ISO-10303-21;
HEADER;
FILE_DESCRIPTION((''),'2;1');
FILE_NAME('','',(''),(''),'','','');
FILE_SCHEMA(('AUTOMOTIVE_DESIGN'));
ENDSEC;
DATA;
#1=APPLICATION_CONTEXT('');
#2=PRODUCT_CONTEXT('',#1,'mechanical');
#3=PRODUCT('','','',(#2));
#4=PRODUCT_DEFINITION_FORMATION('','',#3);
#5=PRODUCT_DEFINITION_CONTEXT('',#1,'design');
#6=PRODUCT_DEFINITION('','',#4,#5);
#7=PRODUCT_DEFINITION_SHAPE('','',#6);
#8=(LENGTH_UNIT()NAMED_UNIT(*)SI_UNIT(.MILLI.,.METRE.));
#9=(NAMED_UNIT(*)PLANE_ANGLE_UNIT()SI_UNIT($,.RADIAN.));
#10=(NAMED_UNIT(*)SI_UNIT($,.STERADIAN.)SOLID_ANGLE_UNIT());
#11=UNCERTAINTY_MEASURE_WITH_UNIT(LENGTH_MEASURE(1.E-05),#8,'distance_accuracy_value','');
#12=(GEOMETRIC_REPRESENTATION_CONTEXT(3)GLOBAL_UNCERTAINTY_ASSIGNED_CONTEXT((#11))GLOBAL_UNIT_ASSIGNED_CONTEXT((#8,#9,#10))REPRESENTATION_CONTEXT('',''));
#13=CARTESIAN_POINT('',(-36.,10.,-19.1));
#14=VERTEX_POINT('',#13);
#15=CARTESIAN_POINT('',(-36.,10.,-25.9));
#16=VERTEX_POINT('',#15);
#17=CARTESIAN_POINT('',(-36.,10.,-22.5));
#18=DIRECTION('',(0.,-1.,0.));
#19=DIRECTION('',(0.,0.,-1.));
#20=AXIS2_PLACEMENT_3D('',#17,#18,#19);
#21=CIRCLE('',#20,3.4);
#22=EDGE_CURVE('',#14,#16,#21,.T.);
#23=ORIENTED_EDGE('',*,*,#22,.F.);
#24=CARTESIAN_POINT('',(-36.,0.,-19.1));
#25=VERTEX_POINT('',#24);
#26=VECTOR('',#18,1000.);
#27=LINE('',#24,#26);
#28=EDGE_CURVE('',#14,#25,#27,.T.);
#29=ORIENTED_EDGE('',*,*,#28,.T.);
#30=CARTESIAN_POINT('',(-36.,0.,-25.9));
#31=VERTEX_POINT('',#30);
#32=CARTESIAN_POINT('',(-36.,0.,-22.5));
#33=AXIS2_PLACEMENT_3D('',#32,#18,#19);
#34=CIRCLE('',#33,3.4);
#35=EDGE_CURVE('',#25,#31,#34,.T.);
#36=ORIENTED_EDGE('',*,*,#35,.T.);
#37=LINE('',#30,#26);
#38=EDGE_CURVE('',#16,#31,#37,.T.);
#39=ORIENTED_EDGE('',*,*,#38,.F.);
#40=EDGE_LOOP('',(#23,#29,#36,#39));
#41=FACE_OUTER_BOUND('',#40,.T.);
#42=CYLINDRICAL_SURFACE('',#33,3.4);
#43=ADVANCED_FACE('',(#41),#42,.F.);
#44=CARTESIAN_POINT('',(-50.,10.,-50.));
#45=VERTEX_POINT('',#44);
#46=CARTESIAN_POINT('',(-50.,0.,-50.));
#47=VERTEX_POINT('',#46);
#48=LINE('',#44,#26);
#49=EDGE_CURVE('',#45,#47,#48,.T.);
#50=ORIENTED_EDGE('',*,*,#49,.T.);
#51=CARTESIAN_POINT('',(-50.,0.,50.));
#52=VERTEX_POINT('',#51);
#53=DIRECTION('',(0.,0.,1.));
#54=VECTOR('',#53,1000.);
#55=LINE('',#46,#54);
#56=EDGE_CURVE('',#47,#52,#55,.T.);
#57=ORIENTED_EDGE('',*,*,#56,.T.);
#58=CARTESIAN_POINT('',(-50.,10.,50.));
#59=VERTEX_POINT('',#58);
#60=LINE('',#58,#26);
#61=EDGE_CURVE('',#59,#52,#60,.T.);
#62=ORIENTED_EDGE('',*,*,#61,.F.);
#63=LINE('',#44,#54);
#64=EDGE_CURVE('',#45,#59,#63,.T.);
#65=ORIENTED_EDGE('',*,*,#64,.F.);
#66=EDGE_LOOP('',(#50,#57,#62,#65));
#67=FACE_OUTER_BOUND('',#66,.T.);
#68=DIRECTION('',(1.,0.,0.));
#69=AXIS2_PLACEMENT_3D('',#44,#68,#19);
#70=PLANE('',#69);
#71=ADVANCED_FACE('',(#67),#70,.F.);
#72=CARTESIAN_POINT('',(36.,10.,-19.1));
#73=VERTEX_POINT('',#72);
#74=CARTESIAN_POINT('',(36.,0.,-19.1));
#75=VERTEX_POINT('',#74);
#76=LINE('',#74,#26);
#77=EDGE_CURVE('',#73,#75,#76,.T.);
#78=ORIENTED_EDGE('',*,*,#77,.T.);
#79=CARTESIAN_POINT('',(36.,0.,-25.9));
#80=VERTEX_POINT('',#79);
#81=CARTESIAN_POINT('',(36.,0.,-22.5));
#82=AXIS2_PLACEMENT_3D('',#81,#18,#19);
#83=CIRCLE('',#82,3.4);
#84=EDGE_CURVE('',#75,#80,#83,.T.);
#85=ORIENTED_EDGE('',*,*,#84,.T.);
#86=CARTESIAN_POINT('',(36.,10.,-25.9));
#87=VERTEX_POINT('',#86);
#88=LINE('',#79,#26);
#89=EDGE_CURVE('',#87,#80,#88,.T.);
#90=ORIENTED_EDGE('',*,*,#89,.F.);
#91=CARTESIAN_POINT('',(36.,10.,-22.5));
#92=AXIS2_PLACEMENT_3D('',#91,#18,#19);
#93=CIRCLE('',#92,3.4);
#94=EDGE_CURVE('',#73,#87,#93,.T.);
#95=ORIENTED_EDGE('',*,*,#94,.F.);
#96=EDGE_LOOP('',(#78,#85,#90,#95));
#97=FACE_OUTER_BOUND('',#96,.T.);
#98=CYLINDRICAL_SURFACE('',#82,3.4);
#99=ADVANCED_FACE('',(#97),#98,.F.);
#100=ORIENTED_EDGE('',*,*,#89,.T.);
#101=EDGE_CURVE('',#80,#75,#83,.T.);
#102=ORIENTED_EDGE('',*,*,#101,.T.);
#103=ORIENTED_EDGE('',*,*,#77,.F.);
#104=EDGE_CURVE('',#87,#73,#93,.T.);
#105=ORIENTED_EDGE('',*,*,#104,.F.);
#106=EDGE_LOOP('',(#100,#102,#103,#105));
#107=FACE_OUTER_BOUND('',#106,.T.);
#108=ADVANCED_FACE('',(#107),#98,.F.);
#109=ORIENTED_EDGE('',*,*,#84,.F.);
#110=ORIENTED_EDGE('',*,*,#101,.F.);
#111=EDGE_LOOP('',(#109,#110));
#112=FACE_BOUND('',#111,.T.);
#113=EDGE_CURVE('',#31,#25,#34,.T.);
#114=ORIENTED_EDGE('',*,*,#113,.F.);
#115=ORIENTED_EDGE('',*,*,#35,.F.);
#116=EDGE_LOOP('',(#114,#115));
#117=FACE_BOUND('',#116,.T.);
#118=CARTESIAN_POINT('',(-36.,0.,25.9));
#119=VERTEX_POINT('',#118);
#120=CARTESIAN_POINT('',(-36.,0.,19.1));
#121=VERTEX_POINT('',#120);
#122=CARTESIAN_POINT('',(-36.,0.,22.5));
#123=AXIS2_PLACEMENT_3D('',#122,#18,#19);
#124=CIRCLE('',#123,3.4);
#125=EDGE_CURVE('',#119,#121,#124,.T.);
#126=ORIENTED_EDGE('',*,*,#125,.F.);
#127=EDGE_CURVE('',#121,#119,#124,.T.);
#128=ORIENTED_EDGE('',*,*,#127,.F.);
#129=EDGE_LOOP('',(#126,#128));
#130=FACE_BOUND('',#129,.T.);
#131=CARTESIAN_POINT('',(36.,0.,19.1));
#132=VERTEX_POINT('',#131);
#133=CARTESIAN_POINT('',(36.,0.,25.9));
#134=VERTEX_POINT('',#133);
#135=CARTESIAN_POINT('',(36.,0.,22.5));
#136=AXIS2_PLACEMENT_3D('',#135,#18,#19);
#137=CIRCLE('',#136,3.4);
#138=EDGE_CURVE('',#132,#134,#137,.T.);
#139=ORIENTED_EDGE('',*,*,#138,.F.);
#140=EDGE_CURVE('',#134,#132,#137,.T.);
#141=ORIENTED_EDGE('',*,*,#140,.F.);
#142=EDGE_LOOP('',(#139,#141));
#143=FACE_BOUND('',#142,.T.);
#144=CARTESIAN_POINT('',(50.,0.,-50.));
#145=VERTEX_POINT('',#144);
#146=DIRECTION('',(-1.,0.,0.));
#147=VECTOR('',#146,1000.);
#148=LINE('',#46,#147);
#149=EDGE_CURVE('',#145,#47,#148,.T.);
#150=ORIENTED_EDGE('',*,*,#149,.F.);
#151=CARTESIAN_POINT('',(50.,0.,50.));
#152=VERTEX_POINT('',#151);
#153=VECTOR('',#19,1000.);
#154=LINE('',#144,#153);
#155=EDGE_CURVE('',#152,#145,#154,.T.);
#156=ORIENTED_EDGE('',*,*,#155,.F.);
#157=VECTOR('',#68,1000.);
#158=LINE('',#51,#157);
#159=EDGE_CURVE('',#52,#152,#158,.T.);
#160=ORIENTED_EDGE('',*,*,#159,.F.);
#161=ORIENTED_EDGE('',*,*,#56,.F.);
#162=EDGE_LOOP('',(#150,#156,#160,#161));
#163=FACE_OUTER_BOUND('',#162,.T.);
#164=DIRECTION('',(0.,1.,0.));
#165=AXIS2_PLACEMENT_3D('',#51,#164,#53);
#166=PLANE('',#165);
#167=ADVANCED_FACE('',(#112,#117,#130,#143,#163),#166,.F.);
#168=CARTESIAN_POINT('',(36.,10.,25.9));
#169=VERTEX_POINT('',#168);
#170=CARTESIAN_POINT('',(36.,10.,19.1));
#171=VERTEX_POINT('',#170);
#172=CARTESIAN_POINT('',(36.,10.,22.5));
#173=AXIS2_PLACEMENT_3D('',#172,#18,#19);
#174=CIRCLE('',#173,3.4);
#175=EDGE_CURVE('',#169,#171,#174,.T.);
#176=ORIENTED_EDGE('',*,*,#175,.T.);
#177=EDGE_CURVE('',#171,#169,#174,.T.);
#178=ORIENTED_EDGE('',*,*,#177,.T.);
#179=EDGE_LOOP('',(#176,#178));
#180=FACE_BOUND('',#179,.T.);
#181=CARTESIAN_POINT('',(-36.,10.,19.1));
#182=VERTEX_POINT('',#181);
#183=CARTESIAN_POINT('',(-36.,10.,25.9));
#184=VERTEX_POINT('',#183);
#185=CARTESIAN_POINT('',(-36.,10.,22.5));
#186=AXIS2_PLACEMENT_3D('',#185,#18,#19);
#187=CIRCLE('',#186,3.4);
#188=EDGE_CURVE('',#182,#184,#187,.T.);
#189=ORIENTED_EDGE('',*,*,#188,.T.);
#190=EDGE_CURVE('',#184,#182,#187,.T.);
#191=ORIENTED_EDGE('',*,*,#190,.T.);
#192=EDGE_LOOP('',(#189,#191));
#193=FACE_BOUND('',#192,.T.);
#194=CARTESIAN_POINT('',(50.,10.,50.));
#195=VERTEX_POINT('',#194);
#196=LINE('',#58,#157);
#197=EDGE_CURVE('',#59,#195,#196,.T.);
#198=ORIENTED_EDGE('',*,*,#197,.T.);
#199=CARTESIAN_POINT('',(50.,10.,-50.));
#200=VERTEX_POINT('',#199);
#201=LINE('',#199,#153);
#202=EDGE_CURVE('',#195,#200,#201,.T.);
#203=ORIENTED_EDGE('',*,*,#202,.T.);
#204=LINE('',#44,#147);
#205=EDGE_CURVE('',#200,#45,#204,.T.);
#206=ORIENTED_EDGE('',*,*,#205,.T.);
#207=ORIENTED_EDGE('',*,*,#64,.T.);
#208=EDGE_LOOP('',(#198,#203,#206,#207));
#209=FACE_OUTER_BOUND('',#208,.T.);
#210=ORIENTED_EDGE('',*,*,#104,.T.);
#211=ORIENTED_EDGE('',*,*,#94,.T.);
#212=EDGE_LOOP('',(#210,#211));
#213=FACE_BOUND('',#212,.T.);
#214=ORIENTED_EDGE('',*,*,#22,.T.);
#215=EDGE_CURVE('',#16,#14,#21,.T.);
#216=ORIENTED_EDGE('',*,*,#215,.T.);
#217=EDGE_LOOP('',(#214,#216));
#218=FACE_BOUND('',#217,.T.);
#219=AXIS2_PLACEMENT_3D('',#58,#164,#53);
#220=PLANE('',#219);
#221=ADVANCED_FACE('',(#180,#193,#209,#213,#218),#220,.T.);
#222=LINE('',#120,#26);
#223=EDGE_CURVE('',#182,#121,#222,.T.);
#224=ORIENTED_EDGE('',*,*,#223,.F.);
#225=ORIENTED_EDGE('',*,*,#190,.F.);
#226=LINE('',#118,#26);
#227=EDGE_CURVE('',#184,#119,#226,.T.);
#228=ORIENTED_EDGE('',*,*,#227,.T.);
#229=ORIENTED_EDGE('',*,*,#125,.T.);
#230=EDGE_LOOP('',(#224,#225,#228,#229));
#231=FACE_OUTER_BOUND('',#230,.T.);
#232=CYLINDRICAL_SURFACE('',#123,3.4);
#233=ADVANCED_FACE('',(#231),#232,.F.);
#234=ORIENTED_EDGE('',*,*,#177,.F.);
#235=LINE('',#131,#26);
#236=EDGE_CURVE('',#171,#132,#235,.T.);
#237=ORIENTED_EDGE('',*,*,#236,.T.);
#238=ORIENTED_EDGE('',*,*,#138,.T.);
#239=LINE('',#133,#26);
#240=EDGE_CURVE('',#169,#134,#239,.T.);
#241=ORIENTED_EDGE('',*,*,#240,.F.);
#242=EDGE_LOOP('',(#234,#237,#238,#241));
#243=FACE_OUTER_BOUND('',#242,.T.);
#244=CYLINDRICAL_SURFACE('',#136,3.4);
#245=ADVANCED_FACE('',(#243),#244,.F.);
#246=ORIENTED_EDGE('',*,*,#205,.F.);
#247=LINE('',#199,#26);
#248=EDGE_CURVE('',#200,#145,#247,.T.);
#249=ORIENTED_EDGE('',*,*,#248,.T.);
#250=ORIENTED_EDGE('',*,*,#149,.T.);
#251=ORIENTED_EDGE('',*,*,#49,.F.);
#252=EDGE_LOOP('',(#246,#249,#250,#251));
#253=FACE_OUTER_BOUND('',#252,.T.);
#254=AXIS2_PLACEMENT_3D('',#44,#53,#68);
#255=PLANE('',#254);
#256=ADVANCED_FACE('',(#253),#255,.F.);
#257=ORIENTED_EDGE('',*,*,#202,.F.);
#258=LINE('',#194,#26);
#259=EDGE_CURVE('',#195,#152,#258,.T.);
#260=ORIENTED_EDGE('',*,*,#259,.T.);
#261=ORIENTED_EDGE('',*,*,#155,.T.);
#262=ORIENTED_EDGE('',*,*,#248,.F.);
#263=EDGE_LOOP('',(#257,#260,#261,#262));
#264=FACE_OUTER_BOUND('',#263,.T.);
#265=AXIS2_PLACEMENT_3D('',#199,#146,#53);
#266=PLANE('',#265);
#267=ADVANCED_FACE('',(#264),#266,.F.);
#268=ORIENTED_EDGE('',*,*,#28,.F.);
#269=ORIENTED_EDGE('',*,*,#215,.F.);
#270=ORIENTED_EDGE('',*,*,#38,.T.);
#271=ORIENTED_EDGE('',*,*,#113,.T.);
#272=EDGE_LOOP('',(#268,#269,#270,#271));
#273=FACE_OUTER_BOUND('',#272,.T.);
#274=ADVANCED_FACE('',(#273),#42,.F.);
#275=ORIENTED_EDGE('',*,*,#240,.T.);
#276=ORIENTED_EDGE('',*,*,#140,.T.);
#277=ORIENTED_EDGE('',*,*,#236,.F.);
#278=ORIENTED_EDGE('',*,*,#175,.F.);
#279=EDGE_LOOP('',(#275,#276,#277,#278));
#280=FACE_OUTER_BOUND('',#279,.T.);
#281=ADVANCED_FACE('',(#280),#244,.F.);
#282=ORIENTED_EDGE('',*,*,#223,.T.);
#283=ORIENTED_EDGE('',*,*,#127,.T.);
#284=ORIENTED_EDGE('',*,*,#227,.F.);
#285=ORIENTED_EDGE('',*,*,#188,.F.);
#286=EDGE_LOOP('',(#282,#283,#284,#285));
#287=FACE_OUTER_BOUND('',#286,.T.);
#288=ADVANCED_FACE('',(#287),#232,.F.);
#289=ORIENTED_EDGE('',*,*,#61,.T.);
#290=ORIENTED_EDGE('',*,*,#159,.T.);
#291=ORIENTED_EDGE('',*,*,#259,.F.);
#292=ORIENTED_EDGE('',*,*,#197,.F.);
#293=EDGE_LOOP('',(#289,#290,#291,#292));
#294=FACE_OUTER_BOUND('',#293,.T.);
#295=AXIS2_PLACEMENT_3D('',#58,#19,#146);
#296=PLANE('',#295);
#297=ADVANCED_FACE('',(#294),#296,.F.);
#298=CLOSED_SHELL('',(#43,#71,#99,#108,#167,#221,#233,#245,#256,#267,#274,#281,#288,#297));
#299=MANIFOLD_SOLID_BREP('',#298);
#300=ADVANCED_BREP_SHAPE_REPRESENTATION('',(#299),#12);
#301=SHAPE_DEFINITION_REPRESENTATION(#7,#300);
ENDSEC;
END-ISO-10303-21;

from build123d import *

# Parameters (mm, degrees)
SKETCH_1_W         = 100
SKETCH_1_H         = 100
EXTRUDE_1_DEPTH    = 10
HOLE_WIZARD_M8_1_D = 6.8


with BuildPart() as part:
    # 草图1 → 拉伸1 (new body)
    with BuildSketch(Plane(origin=(0, 0, 0), x_dir=(1, 0, 0), z_dir=(0, 1, 0))):
        Rectangle(SKETCH_1_W, SKETCH_1_H)
    extrude(amount=EXTRUDE_1_DEPTH)

    # M8 螺纹孔1 (through all)
    with Locations(Plane(origin=(-36, 0, 22.5), x_dir=(0, 0, -1), z_dir=(0, -1, 0))):
        with Locations((0, 0), (45, 0), (0, 72), (45, 72)):
            Hole(HOLE_WIZARD_M8_1_D / 2)


solid = part.part
